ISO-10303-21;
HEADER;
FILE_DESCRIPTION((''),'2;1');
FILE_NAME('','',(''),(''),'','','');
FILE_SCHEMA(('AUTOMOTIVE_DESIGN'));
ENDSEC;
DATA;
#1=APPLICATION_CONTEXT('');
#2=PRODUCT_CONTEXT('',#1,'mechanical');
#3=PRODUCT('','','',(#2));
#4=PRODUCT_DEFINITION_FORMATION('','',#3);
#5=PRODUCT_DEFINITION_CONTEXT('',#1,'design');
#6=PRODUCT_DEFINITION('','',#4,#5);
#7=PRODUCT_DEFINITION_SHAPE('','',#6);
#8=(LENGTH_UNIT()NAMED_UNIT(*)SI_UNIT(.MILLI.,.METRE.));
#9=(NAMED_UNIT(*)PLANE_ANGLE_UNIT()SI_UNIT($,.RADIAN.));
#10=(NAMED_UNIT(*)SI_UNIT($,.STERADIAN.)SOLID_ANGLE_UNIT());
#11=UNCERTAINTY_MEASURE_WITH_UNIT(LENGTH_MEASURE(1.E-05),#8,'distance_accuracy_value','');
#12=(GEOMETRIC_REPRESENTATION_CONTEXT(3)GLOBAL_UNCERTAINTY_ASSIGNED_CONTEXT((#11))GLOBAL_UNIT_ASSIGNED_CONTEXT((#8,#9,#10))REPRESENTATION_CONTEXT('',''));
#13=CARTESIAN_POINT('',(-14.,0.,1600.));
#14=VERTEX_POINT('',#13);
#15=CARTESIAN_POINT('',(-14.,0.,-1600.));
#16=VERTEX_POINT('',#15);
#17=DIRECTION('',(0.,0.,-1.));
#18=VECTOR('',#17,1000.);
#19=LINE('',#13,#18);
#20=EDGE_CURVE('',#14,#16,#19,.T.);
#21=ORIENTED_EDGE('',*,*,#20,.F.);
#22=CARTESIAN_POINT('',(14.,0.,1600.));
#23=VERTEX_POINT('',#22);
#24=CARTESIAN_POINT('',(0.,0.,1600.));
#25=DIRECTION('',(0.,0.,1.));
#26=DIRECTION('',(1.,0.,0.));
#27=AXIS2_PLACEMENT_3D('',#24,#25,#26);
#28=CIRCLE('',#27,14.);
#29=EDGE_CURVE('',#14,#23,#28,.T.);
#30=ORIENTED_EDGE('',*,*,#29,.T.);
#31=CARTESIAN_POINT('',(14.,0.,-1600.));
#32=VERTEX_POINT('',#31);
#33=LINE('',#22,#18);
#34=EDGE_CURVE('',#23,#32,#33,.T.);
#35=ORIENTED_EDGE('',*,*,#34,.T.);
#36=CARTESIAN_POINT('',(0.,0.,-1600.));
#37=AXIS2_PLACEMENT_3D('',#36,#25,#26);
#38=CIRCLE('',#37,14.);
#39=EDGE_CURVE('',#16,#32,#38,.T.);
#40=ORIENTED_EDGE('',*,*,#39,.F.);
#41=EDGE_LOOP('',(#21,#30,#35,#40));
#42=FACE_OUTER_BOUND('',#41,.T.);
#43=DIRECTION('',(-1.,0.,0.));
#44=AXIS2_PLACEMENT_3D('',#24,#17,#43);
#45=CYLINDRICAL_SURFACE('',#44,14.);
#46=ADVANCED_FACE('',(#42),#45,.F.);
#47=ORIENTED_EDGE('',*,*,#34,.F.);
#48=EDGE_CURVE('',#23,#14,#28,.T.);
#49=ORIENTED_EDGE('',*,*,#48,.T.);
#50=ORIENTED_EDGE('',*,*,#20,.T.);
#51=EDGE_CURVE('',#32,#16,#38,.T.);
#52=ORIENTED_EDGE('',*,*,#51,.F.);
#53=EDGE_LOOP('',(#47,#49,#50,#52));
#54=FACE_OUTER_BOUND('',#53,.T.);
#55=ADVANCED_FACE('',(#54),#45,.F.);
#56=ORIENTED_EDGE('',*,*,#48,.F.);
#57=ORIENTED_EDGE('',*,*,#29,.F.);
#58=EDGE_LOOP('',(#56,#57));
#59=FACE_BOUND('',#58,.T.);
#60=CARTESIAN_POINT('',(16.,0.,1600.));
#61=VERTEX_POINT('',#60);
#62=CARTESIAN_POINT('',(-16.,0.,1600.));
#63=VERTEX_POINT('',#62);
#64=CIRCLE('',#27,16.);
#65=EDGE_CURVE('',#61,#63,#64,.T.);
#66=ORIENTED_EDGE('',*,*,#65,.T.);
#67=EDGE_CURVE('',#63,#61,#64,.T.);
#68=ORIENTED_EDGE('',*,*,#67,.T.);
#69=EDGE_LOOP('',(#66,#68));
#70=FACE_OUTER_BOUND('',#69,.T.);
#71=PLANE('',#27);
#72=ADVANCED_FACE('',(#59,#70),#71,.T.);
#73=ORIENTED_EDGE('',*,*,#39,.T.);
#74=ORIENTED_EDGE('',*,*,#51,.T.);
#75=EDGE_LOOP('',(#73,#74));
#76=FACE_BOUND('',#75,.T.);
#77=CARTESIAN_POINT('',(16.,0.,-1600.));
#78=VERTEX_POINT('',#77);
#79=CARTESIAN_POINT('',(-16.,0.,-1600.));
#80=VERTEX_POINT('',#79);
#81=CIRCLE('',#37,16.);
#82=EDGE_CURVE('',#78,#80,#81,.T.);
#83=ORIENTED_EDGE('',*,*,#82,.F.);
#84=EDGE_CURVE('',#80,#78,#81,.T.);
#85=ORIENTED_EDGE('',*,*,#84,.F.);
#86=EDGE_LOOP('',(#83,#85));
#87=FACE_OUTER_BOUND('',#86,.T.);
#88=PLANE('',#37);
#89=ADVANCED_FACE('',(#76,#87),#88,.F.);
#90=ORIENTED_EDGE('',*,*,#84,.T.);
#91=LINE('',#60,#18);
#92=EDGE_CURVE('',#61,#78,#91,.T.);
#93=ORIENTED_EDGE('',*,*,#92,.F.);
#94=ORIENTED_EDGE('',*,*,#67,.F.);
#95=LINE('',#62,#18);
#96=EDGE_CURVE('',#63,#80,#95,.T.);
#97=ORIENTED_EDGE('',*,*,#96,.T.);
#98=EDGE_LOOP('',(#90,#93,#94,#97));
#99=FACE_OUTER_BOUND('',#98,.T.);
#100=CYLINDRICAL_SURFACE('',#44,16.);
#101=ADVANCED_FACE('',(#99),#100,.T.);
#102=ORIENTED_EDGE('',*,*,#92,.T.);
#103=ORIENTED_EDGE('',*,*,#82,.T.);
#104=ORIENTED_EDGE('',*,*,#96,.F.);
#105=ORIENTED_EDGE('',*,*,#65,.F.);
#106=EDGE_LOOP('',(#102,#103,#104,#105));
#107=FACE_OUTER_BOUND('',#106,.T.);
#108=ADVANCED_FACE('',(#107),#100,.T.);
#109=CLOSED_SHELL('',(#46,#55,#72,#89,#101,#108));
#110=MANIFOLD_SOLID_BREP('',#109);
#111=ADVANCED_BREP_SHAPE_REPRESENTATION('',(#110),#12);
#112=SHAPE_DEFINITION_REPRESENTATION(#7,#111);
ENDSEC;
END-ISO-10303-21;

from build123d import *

# Parameters (mm, degrees)
SKETCH_1_R      = 16
SKETCH_1_R_2    = 14
EXTRUDE_1_DEPTH = 1600


with BuildPart() as part:
    # 草图1 → 凸台-拉伸1 (new, symmetric)
    with BuildSketch(Plane.XY):
        Circle(SKETCH_1_R)
        Circle(SKETCH_1_R_2, mode=Mode.SUBTRACT)
    extrude(amount=EXTRUDE_1_DEPTH, both=True)


solid = part.part
